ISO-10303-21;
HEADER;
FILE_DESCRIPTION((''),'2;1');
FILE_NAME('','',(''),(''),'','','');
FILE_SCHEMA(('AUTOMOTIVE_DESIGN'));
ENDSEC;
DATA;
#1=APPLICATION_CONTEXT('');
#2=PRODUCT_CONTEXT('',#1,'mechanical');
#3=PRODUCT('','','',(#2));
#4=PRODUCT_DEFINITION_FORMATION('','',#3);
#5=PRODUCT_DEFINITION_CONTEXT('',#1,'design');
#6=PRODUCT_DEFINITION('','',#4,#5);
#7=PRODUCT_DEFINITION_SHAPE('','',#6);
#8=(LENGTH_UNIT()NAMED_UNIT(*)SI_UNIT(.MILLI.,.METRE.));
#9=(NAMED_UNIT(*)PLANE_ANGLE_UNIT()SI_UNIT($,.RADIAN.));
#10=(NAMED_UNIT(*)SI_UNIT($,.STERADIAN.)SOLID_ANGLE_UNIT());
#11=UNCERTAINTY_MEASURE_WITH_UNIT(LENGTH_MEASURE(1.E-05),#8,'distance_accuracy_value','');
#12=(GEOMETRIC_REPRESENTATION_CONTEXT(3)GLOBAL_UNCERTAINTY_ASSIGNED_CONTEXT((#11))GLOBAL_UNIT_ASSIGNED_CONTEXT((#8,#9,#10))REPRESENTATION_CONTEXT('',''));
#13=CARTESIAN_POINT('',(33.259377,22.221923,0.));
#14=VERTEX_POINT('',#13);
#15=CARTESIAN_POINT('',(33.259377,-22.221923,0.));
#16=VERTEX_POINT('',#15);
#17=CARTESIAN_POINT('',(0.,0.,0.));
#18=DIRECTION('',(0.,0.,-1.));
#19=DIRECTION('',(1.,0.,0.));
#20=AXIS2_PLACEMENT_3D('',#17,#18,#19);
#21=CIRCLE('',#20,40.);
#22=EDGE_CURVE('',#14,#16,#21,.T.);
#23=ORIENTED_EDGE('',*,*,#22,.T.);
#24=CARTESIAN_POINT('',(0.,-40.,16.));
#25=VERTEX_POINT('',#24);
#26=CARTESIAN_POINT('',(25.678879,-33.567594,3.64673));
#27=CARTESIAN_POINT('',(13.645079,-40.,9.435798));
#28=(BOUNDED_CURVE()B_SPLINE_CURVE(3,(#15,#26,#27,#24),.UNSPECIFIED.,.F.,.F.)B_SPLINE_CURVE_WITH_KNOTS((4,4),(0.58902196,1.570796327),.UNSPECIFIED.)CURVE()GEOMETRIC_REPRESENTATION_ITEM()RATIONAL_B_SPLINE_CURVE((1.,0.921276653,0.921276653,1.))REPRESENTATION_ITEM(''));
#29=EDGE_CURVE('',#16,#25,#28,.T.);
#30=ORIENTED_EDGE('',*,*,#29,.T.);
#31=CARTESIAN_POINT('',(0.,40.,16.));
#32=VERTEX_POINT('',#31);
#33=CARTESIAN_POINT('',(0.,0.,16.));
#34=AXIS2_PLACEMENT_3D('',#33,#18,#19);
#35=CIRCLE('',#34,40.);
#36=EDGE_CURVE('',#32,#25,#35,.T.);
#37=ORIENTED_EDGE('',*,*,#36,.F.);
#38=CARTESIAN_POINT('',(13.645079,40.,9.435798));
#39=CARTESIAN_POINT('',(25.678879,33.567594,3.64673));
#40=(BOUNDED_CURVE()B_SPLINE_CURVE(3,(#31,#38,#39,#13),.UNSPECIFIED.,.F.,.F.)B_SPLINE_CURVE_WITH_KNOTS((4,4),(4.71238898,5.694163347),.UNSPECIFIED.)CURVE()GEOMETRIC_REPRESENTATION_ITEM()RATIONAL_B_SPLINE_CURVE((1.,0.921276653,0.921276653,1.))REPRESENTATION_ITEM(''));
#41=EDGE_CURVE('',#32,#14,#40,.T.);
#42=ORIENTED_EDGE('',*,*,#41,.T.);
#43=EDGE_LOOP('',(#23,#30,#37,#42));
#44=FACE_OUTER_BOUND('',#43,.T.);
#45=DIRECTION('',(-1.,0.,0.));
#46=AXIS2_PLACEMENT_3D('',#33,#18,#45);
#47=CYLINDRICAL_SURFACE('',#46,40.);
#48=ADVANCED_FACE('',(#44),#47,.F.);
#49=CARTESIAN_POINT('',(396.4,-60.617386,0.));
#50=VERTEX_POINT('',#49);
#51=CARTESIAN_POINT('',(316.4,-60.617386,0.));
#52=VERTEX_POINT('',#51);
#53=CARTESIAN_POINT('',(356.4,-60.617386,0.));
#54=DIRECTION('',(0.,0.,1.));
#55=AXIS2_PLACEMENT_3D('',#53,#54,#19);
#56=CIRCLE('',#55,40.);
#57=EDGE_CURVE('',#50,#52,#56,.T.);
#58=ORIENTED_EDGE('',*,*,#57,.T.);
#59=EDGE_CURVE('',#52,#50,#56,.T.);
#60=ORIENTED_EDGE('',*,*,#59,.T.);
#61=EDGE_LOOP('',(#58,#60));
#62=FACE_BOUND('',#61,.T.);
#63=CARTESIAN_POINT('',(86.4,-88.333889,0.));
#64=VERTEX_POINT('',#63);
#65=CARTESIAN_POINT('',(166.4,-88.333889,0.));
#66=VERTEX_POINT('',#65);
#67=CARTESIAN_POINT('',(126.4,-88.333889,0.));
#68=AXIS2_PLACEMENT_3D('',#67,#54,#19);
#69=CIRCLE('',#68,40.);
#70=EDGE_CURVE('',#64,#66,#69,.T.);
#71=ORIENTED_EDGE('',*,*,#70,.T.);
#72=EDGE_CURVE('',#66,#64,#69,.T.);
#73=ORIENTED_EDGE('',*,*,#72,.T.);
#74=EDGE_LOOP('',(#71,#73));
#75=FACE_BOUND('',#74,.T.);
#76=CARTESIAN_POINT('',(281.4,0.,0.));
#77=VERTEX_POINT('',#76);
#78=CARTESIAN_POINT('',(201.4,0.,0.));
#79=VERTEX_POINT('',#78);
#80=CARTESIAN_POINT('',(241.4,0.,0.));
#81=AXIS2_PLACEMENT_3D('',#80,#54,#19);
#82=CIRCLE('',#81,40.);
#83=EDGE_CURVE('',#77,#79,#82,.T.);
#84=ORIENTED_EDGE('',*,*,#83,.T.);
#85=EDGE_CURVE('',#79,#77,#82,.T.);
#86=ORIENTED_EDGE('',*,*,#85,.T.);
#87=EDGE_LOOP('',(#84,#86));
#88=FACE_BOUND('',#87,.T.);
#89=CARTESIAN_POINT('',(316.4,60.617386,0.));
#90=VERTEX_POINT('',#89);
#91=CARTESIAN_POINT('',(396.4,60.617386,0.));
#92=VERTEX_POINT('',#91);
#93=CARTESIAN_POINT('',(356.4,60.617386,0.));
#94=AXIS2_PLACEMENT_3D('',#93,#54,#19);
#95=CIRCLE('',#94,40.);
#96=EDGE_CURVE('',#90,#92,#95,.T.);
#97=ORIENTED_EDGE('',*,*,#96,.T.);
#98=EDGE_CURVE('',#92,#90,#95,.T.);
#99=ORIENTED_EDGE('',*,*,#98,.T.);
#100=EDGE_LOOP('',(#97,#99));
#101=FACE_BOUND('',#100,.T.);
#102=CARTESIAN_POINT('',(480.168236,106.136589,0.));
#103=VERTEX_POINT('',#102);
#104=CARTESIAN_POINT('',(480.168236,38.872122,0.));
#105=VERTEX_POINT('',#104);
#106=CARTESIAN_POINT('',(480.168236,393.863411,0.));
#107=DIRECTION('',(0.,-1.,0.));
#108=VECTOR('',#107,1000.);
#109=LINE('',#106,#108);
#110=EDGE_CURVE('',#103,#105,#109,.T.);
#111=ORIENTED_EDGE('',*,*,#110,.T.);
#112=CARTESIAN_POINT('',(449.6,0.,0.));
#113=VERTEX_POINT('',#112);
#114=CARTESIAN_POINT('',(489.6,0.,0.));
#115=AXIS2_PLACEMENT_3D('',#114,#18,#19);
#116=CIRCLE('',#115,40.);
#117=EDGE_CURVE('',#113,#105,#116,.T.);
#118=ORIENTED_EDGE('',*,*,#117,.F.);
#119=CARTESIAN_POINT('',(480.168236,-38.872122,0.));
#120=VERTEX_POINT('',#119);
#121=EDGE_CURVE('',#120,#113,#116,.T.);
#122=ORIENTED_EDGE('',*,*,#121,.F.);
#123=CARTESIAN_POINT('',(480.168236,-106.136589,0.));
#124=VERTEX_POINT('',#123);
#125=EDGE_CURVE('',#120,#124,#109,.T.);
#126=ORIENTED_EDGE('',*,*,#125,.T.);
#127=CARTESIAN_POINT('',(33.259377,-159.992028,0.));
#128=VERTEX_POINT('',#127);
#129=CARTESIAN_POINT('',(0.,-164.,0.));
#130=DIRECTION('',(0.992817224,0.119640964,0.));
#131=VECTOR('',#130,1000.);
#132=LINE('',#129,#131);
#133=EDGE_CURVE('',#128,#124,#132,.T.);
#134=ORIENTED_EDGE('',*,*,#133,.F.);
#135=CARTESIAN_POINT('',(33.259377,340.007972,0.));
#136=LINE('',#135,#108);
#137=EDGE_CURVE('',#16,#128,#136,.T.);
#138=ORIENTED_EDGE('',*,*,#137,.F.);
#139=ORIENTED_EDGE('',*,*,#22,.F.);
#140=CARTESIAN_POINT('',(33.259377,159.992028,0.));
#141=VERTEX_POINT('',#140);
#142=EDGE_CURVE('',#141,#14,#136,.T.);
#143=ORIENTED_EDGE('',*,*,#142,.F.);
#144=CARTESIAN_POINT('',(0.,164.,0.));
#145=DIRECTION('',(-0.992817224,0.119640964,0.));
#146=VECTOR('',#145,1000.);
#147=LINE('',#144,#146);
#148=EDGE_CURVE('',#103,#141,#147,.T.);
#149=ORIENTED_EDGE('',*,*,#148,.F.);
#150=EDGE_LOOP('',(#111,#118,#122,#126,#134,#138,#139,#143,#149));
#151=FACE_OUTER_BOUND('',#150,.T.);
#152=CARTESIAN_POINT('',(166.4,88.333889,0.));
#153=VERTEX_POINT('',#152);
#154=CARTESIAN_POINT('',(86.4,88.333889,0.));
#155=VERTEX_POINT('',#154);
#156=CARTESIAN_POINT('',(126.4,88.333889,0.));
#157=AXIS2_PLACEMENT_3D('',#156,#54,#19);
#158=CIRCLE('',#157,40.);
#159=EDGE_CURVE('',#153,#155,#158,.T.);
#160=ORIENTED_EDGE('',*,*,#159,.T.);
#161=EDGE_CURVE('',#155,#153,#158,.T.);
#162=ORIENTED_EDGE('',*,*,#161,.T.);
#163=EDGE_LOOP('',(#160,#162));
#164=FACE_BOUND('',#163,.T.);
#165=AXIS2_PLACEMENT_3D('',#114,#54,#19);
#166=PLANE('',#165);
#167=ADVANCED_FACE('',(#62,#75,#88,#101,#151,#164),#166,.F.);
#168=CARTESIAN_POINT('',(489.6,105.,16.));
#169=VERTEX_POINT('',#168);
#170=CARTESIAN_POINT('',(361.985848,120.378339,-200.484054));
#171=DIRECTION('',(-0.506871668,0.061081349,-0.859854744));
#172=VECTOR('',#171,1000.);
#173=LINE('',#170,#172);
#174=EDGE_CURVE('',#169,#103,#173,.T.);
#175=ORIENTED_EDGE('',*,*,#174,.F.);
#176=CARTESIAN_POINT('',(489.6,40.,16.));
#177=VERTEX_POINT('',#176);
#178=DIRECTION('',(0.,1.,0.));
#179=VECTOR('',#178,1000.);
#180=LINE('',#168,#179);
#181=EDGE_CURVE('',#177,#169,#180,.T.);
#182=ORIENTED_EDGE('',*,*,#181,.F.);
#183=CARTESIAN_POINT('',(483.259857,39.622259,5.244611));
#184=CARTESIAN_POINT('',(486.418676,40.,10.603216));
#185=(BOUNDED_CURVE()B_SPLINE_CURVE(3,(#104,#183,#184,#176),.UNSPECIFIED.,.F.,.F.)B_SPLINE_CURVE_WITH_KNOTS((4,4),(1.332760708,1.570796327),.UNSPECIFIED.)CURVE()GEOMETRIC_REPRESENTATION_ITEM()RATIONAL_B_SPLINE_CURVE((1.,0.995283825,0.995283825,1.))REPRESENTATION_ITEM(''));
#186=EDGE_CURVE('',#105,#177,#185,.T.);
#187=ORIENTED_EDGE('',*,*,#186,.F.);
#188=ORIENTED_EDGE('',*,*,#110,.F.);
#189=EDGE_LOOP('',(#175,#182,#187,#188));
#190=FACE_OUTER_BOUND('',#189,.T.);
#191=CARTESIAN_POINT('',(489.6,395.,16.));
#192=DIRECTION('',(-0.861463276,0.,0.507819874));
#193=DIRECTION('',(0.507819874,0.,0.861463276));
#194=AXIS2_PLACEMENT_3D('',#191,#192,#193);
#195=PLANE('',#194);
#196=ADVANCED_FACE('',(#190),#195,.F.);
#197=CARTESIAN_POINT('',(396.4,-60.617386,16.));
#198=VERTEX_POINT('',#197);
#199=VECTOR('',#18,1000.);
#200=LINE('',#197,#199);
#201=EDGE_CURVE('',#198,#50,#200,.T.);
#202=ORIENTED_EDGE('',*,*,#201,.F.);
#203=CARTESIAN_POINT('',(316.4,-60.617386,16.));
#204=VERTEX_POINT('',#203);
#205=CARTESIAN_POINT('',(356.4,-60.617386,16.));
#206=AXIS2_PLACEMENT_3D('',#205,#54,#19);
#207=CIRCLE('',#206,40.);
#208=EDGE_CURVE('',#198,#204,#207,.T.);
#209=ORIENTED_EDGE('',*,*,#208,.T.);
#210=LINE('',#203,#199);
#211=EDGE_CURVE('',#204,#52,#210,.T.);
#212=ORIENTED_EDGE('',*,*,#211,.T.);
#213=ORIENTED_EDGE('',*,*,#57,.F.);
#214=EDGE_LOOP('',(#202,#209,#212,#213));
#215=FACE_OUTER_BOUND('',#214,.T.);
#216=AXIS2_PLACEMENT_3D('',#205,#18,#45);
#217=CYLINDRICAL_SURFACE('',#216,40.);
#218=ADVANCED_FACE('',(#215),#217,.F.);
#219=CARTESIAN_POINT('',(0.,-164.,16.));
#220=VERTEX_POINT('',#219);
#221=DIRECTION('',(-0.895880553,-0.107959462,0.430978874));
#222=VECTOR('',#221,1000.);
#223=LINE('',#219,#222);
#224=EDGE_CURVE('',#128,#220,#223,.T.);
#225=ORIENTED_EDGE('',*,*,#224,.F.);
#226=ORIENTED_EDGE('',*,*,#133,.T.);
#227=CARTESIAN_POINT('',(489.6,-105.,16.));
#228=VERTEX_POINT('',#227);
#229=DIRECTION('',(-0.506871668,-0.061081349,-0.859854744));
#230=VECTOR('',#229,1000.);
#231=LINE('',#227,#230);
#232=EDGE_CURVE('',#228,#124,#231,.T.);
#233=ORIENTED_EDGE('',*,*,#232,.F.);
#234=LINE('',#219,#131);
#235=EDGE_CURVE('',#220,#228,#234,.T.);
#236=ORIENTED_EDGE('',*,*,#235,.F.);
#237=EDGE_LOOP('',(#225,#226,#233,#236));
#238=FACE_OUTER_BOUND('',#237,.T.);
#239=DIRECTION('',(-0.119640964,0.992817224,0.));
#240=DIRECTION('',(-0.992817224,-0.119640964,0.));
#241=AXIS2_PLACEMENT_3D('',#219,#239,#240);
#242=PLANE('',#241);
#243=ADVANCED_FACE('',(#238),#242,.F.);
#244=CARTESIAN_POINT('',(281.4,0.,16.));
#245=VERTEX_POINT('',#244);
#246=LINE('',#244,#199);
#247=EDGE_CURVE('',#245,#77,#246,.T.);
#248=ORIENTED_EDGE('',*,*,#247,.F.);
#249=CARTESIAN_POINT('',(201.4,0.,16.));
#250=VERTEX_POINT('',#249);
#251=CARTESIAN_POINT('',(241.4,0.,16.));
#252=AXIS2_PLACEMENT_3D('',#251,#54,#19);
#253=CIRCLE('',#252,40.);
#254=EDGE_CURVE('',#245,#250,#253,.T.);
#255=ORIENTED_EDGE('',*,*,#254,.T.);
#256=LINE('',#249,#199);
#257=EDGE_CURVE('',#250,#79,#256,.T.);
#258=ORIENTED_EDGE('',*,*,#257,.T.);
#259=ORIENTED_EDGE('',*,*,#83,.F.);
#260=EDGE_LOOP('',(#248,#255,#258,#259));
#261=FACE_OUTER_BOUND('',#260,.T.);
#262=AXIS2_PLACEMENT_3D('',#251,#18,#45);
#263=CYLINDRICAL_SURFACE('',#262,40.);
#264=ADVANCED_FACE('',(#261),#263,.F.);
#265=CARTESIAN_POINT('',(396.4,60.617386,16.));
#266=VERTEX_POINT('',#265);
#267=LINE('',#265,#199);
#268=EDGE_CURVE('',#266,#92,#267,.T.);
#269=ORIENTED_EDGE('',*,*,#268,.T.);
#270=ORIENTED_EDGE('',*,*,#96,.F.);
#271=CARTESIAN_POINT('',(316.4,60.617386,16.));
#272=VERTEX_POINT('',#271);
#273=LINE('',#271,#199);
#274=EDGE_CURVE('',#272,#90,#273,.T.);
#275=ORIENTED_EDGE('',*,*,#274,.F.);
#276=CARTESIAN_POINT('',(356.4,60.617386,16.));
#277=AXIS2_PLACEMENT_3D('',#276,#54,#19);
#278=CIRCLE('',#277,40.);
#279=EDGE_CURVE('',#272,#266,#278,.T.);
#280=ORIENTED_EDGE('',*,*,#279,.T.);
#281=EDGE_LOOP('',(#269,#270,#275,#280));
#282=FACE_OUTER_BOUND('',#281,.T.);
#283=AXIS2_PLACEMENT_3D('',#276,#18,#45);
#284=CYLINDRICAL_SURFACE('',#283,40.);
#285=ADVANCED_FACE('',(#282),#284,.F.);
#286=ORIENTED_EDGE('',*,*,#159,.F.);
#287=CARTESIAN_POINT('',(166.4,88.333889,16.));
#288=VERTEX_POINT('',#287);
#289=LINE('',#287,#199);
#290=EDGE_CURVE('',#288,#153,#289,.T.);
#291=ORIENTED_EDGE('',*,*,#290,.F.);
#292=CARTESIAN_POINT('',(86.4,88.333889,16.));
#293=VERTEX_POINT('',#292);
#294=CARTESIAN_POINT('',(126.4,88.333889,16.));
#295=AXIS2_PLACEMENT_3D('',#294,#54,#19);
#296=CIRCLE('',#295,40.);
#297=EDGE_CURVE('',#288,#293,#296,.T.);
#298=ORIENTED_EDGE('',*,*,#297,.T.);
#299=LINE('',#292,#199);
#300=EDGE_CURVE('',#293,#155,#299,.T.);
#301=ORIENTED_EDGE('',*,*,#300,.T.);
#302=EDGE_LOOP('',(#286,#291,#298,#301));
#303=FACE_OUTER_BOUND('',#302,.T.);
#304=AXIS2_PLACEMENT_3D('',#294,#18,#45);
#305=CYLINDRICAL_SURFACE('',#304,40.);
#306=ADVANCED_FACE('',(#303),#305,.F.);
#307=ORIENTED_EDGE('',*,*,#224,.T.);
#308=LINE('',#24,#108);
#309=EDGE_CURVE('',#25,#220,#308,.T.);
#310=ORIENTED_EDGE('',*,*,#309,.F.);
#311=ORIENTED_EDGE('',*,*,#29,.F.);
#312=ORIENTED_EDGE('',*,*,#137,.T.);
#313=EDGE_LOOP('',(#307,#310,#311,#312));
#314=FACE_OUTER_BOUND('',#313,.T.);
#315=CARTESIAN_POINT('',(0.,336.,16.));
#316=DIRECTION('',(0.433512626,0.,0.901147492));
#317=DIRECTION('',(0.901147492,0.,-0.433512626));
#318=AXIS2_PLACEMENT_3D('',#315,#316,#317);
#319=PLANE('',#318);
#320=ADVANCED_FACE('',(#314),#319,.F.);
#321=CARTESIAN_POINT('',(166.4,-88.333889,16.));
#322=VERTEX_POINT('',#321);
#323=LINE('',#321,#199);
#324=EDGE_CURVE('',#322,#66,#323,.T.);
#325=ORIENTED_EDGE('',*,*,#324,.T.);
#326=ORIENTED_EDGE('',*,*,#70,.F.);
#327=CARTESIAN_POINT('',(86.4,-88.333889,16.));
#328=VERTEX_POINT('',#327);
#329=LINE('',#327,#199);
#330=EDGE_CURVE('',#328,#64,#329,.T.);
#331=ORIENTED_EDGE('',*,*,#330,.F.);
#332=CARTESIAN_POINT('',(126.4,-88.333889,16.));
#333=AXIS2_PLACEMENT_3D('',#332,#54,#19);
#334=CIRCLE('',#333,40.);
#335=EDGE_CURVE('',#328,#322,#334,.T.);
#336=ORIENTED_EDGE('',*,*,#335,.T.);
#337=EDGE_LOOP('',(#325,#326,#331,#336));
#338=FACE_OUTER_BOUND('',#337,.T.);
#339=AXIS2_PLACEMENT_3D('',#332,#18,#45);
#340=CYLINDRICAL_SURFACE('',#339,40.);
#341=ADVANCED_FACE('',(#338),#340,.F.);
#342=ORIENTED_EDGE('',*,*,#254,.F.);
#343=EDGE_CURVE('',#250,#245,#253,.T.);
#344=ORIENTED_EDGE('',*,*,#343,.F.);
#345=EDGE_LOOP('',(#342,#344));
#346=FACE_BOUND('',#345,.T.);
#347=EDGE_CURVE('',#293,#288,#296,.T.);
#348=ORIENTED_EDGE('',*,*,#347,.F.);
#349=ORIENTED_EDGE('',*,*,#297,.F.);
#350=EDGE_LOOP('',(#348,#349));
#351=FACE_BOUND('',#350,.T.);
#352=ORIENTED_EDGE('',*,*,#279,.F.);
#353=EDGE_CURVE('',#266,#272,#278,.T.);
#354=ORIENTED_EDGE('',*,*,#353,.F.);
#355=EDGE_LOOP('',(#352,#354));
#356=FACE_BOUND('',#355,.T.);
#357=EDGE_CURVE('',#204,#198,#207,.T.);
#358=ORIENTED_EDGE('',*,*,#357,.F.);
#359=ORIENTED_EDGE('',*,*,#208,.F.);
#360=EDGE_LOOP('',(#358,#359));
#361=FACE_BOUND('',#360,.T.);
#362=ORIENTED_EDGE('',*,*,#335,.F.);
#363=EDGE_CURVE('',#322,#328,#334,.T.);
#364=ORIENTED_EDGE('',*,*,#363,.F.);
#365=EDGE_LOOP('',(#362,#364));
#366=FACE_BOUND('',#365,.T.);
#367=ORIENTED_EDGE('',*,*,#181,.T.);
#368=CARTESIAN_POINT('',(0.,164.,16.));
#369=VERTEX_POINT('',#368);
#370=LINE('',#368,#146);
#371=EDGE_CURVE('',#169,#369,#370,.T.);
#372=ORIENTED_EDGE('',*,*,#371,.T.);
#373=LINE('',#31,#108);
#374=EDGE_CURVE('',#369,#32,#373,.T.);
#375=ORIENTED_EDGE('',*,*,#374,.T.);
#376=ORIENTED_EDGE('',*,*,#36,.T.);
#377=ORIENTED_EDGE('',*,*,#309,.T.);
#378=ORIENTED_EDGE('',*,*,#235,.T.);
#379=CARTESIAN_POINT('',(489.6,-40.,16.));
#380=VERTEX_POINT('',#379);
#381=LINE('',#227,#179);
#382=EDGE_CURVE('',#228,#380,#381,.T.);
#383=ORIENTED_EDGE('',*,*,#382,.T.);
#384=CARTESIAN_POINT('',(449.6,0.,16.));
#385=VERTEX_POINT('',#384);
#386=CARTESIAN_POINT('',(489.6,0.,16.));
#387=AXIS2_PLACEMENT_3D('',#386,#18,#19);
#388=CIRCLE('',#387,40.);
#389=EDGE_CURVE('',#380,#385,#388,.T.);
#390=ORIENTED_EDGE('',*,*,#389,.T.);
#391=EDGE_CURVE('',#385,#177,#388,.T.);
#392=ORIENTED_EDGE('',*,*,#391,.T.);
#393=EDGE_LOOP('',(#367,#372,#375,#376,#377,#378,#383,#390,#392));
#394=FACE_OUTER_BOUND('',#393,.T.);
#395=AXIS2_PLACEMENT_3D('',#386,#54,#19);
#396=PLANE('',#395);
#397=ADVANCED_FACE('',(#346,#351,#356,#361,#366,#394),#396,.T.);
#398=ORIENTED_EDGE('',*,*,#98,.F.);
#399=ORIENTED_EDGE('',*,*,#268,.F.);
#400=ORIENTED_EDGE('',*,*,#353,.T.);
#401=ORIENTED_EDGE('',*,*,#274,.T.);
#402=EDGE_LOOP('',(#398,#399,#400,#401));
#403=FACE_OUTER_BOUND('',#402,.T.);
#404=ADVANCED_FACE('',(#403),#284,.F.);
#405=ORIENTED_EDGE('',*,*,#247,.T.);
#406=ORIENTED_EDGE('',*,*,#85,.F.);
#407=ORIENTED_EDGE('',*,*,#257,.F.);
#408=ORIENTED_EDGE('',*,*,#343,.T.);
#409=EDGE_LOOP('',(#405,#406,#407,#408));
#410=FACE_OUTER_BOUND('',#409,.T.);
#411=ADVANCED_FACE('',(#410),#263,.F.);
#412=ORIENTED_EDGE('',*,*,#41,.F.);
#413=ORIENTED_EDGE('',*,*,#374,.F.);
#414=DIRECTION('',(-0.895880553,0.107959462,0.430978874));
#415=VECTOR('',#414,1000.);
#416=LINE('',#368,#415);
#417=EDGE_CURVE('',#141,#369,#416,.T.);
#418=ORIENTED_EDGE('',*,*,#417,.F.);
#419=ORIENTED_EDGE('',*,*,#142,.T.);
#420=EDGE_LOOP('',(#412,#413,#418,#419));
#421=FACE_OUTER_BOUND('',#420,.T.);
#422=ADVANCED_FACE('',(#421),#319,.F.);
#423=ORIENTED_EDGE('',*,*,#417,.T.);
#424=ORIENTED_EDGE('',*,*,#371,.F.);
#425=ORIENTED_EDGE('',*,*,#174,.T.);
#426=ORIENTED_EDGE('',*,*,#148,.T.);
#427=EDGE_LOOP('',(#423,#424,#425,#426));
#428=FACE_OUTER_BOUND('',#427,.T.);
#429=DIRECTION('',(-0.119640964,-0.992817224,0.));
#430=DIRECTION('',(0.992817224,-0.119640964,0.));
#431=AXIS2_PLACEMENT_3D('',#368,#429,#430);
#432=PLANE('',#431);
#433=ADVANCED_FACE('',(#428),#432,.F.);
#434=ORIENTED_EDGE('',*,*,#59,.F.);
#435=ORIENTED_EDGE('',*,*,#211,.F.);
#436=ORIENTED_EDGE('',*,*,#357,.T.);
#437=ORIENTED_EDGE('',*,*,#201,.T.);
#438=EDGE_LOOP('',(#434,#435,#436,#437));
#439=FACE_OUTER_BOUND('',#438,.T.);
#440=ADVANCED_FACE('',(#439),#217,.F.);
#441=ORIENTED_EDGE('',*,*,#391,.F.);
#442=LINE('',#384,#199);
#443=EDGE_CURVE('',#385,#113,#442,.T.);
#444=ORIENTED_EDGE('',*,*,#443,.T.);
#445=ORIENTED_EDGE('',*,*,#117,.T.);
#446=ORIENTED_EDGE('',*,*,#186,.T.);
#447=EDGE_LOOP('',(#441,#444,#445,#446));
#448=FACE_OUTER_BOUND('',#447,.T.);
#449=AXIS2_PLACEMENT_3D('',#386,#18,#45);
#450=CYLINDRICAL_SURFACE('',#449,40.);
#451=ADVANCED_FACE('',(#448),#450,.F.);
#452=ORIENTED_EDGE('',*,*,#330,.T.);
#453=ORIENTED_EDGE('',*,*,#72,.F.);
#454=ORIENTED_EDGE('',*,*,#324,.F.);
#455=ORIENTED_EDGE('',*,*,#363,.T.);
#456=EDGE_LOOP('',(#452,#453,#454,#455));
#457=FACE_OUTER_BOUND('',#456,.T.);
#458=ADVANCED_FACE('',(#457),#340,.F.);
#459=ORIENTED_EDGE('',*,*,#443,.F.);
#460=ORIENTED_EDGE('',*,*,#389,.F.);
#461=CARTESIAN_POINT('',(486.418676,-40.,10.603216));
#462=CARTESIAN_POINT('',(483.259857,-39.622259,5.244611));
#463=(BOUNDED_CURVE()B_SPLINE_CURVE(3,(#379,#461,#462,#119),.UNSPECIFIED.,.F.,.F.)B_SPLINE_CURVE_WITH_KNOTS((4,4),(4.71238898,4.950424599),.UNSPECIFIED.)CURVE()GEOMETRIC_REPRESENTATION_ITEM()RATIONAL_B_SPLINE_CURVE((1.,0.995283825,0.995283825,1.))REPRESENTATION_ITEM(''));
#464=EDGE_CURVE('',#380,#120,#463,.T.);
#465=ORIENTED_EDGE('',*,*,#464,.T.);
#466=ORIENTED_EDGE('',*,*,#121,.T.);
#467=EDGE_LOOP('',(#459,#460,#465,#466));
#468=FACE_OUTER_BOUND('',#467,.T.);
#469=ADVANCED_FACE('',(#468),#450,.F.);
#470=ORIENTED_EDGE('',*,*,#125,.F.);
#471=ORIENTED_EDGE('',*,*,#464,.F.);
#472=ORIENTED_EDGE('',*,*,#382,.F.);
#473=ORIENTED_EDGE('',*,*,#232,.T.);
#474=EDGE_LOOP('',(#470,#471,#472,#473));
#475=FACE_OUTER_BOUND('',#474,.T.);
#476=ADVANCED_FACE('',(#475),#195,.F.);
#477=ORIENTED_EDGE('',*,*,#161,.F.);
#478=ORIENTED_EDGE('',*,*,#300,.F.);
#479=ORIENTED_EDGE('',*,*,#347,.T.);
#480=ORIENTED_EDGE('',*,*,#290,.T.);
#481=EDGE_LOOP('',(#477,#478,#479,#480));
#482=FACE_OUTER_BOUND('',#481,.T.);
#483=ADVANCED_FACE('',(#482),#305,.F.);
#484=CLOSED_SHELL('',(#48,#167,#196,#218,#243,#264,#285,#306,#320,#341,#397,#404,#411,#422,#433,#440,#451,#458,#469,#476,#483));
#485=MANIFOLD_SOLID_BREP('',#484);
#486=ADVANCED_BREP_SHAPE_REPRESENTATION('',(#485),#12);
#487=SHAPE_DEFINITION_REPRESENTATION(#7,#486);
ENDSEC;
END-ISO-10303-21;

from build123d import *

# Parameters (mm, degrees)
SKETCH1_R           = 40
BOSS_EXTRUDE1_DEPTH = 16
CUT_EXTRUDE2_DEPTH  = 500


with BuildPart() as part:
    # Sketch1 → Boss-Extrude1 (new body)
    with BuildSketch(Plane.XY):
        with BuildLine():
            Line((0, 40), (0, 164))
            Line((0, 164), (489.6, 105))
            Line((489.6, 105), (489.6, 40))
            ThreePointArc((489.6, 40), (449.6, 0), (489.6, -40))
            Line((489.6, -40), (489.6, -105))
            Line((489.6, -105), (0, -164))
            Line((0, -164), (0, -40))
            ThreePointArc((0, -40), (40, 0), (0, 40))
        make_face()
        with Locations((241.4, 0)):
            Circle(SKETCH1_R, mode=Mode.SUBTRACT)
        with Locations((126.4, 88.333889345)):
            Circle(SKETCH1_R, mode=Mode.SUBTRACT)
        with Locations((356.4, 60.617386077)):
            Circle(SKETCH1_R, mode=Mode.SUBTRACT)
        with Locations((126.4, -88.333889345)):
            Circle(SKETCH1_R, mode=Mode.SUBTRACT)
        with Locations((356.4, -60.617386077)):
            Circle(SKETCH1_R, mode=Mode.SUBTRACT)
    extrude(amount=BOSS_EXTRUDE1_DEPTH)

    # Sketch3 → Cut-Extrude2 (cut, along a direction that is not the sketch's normal)
    with BuildSketch(Plane(origin=(19.480184067, -161.652510498, 0), x_dir=(0.9928172236743598, 0.11964096445422229, 0), z_dir=(0.11964096445422229, -0.9928172236743598, 0))):
        Polygon((473.521011443, 16), (464.021011443, 0), (473.521011443, 0), align=None)
        Polygon((-19.62111817, 16), (-19.62111817, 0), (13.87888183, 0), align=None)
    extrude(amount=-CUT_EXTRUDE2_DEPTH, dir=(0, -1, 0), mode=Mode.SUBTRACT)


solid = part.part
